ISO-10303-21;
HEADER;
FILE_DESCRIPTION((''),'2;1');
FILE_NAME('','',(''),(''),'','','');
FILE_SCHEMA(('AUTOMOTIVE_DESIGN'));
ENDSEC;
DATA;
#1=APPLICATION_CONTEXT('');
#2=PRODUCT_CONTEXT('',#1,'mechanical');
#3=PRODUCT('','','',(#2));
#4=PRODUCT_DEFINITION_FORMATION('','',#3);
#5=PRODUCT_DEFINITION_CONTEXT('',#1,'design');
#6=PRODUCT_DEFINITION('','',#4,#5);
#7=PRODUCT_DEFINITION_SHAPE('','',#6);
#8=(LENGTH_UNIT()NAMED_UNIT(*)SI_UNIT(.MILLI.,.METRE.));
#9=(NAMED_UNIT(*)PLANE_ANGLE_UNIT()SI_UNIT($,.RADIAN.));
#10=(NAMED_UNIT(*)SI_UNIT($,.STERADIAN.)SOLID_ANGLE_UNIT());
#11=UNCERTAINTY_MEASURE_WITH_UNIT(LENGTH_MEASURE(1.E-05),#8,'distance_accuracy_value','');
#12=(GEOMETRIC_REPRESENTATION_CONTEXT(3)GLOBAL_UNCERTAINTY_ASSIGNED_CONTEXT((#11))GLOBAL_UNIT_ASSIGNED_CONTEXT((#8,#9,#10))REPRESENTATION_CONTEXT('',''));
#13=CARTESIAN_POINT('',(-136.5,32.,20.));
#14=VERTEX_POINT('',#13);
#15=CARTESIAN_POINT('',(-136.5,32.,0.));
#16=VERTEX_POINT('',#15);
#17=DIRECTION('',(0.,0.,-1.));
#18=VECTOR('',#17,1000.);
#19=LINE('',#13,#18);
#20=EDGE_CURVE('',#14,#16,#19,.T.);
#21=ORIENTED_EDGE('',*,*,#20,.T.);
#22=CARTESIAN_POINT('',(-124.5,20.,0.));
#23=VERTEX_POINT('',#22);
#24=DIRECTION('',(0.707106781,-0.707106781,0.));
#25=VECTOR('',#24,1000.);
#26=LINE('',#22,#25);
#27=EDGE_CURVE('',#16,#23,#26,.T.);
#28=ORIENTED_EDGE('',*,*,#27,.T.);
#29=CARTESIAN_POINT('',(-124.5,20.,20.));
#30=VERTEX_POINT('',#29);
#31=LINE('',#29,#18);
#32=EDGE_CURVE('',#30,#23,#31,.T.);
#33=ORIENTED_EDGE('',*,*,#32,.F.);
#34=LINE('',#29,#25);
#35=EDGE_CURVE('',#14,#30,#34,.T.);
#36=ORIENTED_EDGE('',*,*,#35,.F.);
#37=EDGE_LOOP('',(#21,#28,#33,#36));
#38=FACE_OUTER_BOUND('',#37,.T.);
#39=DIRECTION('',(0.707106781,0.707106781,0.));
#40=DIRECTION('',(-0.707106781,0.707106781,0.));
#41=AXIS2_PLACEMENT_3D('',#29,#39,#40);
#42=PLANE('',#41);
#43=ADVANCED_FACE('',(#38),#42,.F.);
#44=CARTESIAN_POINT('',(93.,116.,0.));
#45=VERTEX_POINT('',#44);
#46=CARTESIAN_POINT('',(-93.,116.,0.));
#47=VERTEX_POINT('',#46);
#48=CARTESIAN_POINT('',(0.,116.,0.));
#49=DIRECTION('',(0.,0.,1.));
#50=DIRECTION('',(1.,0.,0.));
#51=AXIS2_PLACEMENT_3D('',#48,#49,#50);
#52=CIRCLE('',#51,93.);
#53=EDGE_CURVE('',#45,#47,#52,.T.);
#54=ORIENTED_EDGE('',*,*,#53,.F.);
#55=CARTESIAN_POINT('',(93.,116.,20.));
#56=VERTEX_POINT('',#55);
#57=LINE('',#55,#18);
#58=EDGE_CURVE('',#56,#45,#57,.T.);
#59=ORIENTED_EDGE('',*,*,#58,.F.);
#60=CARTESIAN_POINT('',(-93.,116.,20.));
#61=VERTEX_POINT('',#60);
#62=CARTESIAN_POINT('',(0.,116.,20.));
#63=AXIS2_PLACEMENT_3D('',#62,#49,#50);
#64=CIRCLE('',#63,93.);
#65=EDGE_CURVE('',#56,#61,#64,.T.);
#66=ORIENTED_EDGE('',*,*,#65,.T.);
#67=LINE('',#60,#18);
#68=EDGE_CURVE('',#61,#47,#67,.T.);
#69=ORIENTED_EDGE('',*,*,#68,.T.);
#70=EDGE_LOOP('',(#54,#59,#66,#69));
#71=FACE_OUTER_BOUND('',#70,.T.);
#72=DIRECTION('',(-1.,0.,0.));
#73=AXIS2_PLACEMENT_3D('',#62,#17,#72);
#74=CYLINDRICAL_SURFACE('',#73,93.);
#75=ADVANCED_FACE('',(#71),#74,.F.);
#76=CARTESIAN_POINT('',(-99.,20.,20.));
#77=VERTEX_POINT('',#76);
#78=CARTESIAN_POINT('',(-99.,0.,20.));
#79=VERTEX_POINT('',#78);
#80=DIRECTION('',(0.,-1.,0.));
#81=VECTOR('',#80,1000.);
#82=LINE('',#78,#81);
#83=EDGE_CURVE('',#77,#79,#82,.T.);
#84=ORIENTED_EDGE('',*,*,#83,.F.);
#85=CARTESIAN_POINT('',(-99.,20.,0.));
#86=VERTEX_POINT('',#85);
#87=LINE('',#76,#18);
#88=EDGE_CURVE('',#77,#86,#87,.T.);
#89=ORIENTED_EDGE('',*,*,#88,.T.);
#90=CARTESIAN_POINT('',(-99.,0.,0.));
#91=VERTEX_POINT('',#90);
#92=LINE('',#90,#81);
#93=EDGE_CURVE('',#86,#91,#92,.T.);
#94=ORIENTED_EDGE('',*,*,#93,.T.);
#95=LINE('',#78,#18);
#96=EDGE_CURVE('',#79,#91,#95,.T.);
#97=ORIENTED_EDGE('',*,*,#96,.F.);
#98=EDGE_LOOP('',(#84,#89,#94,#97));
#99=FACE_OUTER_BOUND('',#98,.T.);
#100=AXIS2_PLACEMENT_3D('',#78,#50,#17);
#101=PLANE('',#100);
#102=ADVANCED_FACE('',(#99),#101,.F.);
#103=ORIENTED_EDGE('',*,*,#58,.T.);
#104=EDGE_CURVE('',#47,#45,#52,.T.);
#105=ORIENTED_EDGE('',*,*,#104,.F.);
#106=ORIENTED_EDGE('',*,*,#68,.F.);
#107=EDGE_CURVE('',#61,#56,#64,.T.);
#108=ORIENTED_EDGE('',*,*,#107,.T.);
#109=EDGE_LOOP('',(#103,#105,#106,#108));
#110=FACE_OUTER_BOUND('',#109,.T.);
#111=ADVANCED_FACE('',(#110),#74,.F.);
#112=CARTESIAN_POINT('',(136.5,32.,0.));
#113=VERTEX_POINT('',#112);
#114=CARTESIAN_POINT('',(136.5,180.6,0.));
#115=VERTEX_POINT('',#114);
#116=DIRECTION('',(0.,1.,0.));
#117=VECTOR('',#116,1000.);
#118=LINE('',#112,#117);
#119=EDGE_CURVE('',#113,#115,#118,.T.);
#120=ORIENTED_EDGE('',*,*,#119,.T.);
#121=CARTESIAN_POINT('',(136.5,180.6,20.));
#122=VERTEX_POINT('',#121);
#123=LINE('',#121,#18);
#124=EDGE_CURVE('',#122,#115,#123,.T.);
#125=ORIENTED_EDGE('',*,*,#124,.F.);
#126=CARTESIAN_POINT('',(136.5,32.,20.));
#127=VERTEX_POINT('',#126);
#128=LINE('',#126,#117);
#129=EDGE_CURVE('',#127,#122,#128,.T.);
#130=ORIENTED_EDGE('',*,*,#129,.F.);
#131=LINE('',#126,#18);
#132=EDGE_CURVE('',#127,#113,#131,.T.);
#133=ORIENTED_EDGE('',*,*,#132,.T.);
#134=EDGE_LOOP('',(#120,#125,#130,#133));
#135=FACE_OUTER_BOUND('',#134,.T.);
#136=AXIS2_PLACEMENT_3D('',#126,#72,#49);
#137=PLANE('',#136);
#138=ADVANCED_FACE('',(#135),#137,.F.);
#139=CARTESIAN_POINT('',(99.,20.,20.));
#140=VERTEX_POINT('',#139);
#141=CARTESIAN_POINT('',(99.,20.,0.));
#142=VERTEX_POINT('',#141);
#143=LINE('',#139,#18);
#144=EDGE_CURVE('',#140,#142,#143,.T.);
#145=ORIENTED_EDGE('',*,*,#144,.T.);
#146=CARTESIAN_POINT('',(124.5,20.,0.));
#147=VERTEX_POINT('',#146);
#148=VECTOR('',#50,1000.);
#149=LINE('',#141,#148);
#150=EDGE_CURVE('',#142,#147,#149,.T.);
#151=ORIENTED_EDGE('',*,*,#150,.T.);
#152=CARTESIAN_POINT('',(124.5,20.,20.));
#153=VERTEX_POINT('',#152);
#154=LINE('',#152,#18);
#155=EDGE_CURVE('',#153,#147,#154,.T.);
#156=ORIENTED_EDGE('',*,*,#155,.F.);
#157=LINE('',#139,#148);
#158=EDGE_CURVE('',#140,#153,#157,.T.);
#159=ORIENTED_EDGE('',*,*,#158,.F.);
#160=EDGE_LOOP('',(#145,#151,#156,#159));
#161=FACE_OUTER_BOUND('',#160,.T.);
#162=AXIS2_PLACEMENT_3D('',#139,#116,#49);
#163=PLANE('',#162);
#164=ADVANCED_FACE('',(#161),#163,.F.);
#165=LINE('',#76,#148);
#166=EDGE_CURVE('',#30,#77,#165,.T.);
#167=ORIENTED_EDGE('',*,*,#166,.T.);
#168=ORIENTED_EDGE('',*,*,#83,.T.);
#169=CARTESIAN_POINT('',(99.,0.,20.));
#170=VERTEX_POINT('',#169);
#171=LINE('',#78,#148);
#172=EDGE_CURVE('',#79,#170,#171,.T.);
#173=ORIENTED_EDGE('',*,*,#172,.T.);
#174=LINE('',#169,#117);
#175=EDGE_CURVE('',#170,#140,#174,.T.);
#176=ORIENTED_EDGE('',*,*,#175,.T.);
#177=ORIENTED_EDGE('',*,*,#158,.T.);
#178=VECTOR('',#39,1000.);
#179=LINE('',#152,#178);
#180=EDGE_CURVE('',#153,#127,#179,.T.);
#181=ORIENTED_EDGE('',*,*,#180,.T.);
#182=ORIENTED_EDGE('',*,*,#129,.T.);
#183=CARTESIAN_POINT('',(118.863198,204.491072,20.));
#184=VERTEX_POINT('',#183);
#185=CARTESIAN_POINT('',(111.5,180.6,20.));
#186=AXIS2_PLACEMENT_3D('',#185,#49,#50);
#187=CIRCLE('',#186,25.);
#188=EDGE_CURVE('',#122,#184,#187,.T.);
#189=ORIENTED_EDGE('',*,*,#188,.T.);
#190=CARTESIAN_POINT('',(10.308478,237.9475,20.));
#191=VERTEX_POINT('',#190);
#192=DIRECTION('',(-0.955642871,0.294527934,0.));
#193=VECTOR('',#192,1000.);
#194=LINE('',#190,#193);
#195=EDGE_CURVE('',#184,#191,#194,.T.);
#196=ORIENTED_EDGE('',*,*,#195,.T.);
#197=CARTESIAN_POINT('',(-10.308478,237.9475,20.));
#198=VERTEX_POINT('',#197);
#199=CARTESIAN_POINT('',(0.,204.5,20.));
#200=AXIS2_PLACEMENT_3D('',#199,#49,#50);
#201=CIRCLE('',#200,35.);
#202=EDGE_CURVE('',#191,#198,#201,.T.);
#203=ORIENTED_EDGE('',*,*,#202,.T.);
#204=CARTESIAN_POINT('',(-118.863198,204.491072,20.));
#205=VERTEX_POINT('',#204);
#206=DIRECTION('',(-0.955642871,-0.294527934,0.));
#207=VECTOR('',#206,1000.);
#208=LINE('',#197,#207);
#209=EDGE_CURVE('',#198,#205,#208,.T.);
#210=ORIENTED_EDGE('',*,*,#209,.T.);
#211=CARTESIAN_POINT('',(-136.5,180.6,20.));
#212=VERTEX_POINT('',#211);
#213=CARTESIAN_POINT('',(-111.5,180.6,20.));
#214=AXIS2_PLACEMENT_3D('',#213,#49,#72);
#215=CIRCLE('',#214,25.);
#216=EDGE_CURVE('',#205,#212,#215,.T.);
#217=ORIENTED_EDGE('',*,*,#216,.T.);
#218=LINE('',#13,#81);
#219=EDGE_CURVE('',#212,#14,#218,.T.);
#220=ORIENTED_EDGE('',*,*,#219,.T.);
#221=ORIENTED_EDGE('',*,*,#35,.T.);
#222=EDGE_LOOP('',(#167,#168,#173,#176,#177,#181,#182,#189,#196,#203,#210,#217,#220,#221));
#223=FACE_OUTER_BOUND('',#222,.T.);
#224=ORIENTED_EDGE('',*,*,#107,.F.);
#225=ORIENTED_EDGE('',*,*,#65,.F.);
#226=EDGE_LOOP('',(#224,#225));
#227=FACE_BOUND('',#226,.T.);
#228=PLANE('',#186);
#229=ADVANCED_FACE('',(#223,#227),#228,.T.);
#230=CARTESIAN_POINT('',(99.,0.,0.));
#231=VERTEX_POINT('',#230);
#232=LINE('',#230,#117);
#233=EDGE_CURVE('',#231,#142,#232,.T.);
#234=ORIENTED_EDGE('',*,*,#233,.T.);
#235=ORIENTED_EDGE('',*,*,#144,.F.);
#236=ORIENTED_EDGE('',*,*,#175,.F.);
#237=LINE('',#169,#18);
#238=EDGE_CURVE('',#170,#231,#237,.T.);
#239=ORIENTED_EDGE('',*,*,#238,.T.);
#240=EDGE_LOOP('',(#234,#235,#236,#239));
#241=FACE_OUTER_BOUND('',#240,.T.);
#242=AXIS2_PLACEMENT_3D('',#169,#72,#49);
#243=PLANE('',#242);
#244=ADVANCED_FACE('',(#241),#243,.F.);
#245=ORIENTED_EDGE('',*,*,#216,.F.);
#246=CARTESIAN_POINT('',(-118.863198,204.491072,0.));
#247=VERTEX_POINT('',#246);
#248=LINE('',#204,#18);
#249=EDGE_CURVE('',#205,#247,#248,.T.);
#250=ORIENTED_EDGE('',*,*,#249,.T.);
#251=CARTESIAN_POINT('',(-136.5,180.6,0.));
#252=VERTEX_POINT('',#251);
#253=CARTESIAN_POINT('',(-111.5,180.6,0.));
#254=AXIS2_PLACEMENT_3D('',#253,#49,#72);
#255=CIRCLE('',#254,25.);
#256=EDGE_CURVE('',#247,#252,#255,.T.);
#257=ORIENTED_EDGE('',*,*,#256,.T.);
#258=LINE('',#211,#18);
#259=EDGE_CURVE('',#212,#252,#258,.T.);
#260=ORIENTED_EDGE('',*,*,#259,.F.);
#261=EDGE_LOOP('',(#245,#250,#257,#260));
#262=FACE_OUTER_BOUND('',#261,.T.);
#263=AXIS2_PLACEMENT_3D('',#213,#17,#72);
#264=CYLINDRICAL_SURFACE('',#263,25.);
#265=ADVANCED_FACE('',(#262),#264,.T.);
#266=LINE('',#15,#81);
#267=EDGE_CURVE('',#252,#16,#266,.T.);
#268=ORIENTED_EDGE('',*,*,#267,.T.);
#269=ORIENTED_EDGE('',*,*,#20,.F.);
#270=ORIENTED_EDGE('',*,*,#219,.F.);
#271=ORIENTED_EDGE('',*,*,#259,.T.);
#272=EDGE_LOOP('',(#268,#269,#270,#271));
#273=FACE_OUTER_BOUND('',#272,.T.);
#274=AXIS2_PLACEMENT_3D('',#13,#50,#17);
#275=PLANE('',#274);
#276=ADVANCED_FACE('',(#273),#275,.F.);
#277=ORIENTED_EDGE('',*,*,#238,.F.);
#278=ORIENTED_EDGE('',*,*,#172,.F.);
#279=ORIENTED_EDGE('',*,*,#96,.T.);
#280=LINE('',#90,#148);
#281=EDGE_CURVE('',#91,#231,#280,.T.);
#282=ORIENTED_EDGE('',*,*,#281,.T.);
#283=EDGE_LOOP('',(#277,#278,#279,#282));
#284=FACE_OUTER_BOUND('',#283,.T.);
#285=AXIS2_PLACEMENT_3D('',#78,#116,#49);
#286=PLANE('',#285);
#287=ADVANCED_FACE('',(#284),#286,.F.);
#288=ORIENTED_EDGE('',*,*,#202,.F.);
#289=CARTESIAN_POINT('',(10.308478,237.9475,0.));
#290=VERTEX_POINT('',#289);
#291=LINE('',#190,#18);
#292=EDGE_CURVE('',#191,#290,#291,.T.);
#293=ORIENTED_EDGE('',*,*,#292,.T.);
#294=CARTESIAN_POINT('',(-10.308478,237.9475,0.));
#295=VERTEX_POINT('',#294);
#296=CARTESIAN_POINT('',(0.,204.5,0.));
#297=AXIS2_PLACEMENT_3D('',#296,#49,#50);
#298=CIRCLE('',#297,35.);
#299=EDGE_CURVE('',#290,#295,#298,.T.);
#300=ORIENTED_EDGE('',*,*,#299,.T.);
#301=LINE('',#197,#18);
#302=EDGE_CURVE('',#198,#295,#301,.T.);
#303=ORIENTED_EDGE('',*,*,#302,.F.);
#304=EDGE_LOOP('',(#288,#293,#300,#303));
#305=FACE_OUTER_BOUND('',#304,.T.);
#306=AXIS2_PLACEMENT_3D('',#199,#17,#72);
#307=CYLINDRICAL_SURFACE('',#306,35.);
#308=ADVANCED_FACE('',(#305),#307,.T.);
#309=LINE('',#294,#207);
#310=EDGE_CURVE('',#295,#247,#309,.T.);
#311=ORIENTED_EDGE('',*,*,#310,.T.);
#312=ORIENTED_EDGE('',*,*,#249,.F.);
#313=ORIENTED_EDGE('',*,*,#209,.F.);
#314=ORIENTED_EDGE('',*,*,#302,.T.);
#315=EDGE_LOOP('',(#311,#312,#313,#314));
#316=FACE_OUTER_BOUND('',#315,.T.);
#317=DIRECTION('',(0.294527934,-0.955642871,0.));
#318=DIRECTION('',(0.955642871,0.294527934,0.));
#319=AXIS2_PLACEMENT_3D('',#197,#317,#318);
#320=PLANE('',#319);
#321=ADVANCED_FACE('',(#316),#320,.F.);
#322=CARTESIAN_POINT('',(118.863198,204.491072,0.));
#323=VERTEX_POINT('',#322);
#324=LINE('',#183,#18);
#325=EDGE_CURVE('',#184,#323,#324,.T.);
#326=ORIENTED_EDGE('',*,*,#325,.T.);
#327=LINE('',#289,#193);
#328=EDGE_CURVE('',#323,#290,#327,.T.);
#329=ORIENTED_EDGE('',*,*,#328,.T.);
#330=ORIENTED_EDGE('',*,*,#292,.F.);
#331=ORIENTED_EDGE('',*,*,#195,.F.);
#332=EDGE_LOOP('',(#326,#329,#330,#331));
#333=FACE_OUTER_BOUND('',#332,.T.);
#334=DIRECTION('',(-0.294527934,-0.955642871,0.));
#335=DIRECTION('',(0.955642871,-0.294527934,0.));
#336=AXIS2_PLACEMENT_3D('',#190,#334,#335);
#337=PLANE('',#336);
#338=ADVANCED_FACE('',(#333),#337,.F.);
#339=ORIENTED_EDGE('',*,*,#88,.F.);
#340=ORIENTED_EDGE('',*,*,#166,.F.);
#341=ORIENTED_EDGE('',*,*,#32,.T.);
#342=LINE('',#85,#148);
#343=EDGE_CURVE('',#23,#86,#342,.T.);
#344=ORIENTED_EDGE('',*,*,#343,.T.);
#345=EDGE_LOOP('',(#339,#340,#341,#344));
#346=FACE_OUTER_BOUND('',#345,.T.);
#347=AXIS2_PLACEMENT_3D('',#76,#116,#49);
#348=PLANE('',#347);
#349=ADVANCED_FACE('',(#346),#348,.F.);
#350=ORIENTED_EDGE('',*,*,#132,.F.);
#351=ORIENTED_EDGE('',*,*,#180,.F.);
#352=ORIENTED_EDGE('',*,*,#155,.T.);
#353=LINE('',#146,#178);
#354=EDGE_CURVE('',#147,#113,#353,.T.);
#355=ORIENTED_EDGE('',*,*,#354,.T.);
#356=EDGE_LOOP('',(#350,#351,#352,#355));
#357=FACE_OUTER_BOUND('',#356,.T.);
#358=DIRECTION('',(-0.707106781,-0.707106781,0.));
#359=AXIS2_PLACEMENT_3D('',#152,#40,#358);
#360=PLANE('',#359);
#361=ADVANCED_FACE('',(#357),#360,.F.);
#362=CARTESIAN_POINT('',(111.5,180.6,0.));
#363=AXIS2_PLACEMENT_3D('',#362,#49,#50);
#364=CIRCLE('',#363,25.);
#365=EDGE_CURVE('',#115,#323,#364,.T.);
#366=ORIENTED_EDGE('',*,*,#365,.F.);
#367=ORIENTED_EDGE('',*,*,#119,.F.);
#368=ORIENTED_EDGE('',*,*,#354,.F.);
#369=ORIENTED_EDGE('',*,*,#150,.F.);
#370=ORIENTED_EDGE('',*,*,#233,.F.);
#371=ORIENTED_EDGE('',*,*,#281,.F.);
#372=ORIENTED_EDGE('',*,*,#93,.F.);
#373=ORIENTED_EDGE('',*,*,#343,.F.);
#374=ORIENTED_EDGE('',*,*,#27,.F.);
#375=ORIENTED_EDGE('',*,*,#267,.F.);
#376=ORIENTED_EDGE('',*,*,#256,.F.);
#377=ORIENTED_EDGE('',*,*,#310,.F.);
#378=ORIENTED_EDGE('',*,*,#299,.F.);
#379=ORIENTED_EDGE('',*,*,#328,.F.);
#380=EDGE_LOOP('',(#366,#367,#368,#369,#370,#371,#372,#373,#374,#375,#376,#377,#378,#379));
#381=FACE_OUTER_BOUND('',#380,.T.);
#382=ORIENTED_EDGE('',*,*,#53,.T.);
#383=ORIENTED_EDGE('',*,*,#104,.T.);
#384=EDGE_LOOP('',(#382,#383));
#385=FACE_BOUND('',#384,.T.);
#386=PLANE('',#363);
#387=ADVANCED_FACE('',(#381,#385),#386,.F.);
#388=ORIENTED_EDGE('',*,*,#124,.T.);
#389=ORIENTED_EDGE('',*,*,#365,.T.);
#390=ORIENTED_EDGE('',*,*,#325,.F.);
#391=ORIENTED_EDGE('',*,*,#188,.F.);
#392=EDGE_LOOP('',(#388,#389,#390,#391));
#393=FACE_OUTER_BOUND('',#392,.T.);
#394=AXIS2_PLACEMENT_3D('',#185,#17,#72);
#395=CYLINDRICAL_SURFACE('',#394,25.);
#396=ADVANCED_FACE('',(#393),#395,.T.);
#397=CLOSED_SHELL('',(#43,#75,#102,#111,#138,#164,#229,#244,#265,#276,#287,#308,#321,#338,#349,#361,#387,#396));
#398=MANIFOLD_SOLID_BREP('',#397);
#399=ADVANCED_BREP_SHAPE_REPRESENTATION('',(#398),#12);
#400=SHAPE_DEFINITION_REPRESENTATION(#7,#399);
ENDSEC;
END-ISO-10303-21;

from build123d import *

# Parameters (mm, degrees)
SKETCH1_R           = 93
BOSS_EXTRUDE1_DEPTH = 20


with BuildPart() as part:
    # Sketch1 → Boss-Extrude1 (new body)
    with BuildSketch(Plane.XY):
        with BuildLine():
            Line((-99, 0), (99, 0))
            Line((99, 0), (99, 20))
            Line((99, 20), (124.5, 20))
            Line((124.5, 20), (136.5, 32))
            Line((136.5, 32), (136.5, 180.6))
            ThreePointArc((136.5, 180.6), (131.613179244, 195.447896171), (118.863198343, 204.491071767))
            Line((118.863198343, 204.491071767), (10.30847768, 237.947500473))
            ThreePointArc((10.30847768, 237.947500473), (0, 239.5), (-10.30847768, 237.947500473))
            Line((-10.30847768, 237.947500473), (-118.863198343, 204.491071767))
            ThreePointArc((-118.863198343, 204.491071767), (-131.613179244, 195.447896171), (-136.5, 180.6))
            Line((-136.5, 180.6), (-136.5, 32))
            Line((-136.5, 32), (-124.5, 20))
            Line((-124.5, 20), (-99, 20))
            Line((-99, 20), (-99, 0))
        make_face()
        with Locations((0, 116)):
            Circle(SKETCH1_R, mode=Mode.SUBTRACT)
    extrude(amount=BOSS_EXTRUDE1_DEPTH)


solid = part.part
